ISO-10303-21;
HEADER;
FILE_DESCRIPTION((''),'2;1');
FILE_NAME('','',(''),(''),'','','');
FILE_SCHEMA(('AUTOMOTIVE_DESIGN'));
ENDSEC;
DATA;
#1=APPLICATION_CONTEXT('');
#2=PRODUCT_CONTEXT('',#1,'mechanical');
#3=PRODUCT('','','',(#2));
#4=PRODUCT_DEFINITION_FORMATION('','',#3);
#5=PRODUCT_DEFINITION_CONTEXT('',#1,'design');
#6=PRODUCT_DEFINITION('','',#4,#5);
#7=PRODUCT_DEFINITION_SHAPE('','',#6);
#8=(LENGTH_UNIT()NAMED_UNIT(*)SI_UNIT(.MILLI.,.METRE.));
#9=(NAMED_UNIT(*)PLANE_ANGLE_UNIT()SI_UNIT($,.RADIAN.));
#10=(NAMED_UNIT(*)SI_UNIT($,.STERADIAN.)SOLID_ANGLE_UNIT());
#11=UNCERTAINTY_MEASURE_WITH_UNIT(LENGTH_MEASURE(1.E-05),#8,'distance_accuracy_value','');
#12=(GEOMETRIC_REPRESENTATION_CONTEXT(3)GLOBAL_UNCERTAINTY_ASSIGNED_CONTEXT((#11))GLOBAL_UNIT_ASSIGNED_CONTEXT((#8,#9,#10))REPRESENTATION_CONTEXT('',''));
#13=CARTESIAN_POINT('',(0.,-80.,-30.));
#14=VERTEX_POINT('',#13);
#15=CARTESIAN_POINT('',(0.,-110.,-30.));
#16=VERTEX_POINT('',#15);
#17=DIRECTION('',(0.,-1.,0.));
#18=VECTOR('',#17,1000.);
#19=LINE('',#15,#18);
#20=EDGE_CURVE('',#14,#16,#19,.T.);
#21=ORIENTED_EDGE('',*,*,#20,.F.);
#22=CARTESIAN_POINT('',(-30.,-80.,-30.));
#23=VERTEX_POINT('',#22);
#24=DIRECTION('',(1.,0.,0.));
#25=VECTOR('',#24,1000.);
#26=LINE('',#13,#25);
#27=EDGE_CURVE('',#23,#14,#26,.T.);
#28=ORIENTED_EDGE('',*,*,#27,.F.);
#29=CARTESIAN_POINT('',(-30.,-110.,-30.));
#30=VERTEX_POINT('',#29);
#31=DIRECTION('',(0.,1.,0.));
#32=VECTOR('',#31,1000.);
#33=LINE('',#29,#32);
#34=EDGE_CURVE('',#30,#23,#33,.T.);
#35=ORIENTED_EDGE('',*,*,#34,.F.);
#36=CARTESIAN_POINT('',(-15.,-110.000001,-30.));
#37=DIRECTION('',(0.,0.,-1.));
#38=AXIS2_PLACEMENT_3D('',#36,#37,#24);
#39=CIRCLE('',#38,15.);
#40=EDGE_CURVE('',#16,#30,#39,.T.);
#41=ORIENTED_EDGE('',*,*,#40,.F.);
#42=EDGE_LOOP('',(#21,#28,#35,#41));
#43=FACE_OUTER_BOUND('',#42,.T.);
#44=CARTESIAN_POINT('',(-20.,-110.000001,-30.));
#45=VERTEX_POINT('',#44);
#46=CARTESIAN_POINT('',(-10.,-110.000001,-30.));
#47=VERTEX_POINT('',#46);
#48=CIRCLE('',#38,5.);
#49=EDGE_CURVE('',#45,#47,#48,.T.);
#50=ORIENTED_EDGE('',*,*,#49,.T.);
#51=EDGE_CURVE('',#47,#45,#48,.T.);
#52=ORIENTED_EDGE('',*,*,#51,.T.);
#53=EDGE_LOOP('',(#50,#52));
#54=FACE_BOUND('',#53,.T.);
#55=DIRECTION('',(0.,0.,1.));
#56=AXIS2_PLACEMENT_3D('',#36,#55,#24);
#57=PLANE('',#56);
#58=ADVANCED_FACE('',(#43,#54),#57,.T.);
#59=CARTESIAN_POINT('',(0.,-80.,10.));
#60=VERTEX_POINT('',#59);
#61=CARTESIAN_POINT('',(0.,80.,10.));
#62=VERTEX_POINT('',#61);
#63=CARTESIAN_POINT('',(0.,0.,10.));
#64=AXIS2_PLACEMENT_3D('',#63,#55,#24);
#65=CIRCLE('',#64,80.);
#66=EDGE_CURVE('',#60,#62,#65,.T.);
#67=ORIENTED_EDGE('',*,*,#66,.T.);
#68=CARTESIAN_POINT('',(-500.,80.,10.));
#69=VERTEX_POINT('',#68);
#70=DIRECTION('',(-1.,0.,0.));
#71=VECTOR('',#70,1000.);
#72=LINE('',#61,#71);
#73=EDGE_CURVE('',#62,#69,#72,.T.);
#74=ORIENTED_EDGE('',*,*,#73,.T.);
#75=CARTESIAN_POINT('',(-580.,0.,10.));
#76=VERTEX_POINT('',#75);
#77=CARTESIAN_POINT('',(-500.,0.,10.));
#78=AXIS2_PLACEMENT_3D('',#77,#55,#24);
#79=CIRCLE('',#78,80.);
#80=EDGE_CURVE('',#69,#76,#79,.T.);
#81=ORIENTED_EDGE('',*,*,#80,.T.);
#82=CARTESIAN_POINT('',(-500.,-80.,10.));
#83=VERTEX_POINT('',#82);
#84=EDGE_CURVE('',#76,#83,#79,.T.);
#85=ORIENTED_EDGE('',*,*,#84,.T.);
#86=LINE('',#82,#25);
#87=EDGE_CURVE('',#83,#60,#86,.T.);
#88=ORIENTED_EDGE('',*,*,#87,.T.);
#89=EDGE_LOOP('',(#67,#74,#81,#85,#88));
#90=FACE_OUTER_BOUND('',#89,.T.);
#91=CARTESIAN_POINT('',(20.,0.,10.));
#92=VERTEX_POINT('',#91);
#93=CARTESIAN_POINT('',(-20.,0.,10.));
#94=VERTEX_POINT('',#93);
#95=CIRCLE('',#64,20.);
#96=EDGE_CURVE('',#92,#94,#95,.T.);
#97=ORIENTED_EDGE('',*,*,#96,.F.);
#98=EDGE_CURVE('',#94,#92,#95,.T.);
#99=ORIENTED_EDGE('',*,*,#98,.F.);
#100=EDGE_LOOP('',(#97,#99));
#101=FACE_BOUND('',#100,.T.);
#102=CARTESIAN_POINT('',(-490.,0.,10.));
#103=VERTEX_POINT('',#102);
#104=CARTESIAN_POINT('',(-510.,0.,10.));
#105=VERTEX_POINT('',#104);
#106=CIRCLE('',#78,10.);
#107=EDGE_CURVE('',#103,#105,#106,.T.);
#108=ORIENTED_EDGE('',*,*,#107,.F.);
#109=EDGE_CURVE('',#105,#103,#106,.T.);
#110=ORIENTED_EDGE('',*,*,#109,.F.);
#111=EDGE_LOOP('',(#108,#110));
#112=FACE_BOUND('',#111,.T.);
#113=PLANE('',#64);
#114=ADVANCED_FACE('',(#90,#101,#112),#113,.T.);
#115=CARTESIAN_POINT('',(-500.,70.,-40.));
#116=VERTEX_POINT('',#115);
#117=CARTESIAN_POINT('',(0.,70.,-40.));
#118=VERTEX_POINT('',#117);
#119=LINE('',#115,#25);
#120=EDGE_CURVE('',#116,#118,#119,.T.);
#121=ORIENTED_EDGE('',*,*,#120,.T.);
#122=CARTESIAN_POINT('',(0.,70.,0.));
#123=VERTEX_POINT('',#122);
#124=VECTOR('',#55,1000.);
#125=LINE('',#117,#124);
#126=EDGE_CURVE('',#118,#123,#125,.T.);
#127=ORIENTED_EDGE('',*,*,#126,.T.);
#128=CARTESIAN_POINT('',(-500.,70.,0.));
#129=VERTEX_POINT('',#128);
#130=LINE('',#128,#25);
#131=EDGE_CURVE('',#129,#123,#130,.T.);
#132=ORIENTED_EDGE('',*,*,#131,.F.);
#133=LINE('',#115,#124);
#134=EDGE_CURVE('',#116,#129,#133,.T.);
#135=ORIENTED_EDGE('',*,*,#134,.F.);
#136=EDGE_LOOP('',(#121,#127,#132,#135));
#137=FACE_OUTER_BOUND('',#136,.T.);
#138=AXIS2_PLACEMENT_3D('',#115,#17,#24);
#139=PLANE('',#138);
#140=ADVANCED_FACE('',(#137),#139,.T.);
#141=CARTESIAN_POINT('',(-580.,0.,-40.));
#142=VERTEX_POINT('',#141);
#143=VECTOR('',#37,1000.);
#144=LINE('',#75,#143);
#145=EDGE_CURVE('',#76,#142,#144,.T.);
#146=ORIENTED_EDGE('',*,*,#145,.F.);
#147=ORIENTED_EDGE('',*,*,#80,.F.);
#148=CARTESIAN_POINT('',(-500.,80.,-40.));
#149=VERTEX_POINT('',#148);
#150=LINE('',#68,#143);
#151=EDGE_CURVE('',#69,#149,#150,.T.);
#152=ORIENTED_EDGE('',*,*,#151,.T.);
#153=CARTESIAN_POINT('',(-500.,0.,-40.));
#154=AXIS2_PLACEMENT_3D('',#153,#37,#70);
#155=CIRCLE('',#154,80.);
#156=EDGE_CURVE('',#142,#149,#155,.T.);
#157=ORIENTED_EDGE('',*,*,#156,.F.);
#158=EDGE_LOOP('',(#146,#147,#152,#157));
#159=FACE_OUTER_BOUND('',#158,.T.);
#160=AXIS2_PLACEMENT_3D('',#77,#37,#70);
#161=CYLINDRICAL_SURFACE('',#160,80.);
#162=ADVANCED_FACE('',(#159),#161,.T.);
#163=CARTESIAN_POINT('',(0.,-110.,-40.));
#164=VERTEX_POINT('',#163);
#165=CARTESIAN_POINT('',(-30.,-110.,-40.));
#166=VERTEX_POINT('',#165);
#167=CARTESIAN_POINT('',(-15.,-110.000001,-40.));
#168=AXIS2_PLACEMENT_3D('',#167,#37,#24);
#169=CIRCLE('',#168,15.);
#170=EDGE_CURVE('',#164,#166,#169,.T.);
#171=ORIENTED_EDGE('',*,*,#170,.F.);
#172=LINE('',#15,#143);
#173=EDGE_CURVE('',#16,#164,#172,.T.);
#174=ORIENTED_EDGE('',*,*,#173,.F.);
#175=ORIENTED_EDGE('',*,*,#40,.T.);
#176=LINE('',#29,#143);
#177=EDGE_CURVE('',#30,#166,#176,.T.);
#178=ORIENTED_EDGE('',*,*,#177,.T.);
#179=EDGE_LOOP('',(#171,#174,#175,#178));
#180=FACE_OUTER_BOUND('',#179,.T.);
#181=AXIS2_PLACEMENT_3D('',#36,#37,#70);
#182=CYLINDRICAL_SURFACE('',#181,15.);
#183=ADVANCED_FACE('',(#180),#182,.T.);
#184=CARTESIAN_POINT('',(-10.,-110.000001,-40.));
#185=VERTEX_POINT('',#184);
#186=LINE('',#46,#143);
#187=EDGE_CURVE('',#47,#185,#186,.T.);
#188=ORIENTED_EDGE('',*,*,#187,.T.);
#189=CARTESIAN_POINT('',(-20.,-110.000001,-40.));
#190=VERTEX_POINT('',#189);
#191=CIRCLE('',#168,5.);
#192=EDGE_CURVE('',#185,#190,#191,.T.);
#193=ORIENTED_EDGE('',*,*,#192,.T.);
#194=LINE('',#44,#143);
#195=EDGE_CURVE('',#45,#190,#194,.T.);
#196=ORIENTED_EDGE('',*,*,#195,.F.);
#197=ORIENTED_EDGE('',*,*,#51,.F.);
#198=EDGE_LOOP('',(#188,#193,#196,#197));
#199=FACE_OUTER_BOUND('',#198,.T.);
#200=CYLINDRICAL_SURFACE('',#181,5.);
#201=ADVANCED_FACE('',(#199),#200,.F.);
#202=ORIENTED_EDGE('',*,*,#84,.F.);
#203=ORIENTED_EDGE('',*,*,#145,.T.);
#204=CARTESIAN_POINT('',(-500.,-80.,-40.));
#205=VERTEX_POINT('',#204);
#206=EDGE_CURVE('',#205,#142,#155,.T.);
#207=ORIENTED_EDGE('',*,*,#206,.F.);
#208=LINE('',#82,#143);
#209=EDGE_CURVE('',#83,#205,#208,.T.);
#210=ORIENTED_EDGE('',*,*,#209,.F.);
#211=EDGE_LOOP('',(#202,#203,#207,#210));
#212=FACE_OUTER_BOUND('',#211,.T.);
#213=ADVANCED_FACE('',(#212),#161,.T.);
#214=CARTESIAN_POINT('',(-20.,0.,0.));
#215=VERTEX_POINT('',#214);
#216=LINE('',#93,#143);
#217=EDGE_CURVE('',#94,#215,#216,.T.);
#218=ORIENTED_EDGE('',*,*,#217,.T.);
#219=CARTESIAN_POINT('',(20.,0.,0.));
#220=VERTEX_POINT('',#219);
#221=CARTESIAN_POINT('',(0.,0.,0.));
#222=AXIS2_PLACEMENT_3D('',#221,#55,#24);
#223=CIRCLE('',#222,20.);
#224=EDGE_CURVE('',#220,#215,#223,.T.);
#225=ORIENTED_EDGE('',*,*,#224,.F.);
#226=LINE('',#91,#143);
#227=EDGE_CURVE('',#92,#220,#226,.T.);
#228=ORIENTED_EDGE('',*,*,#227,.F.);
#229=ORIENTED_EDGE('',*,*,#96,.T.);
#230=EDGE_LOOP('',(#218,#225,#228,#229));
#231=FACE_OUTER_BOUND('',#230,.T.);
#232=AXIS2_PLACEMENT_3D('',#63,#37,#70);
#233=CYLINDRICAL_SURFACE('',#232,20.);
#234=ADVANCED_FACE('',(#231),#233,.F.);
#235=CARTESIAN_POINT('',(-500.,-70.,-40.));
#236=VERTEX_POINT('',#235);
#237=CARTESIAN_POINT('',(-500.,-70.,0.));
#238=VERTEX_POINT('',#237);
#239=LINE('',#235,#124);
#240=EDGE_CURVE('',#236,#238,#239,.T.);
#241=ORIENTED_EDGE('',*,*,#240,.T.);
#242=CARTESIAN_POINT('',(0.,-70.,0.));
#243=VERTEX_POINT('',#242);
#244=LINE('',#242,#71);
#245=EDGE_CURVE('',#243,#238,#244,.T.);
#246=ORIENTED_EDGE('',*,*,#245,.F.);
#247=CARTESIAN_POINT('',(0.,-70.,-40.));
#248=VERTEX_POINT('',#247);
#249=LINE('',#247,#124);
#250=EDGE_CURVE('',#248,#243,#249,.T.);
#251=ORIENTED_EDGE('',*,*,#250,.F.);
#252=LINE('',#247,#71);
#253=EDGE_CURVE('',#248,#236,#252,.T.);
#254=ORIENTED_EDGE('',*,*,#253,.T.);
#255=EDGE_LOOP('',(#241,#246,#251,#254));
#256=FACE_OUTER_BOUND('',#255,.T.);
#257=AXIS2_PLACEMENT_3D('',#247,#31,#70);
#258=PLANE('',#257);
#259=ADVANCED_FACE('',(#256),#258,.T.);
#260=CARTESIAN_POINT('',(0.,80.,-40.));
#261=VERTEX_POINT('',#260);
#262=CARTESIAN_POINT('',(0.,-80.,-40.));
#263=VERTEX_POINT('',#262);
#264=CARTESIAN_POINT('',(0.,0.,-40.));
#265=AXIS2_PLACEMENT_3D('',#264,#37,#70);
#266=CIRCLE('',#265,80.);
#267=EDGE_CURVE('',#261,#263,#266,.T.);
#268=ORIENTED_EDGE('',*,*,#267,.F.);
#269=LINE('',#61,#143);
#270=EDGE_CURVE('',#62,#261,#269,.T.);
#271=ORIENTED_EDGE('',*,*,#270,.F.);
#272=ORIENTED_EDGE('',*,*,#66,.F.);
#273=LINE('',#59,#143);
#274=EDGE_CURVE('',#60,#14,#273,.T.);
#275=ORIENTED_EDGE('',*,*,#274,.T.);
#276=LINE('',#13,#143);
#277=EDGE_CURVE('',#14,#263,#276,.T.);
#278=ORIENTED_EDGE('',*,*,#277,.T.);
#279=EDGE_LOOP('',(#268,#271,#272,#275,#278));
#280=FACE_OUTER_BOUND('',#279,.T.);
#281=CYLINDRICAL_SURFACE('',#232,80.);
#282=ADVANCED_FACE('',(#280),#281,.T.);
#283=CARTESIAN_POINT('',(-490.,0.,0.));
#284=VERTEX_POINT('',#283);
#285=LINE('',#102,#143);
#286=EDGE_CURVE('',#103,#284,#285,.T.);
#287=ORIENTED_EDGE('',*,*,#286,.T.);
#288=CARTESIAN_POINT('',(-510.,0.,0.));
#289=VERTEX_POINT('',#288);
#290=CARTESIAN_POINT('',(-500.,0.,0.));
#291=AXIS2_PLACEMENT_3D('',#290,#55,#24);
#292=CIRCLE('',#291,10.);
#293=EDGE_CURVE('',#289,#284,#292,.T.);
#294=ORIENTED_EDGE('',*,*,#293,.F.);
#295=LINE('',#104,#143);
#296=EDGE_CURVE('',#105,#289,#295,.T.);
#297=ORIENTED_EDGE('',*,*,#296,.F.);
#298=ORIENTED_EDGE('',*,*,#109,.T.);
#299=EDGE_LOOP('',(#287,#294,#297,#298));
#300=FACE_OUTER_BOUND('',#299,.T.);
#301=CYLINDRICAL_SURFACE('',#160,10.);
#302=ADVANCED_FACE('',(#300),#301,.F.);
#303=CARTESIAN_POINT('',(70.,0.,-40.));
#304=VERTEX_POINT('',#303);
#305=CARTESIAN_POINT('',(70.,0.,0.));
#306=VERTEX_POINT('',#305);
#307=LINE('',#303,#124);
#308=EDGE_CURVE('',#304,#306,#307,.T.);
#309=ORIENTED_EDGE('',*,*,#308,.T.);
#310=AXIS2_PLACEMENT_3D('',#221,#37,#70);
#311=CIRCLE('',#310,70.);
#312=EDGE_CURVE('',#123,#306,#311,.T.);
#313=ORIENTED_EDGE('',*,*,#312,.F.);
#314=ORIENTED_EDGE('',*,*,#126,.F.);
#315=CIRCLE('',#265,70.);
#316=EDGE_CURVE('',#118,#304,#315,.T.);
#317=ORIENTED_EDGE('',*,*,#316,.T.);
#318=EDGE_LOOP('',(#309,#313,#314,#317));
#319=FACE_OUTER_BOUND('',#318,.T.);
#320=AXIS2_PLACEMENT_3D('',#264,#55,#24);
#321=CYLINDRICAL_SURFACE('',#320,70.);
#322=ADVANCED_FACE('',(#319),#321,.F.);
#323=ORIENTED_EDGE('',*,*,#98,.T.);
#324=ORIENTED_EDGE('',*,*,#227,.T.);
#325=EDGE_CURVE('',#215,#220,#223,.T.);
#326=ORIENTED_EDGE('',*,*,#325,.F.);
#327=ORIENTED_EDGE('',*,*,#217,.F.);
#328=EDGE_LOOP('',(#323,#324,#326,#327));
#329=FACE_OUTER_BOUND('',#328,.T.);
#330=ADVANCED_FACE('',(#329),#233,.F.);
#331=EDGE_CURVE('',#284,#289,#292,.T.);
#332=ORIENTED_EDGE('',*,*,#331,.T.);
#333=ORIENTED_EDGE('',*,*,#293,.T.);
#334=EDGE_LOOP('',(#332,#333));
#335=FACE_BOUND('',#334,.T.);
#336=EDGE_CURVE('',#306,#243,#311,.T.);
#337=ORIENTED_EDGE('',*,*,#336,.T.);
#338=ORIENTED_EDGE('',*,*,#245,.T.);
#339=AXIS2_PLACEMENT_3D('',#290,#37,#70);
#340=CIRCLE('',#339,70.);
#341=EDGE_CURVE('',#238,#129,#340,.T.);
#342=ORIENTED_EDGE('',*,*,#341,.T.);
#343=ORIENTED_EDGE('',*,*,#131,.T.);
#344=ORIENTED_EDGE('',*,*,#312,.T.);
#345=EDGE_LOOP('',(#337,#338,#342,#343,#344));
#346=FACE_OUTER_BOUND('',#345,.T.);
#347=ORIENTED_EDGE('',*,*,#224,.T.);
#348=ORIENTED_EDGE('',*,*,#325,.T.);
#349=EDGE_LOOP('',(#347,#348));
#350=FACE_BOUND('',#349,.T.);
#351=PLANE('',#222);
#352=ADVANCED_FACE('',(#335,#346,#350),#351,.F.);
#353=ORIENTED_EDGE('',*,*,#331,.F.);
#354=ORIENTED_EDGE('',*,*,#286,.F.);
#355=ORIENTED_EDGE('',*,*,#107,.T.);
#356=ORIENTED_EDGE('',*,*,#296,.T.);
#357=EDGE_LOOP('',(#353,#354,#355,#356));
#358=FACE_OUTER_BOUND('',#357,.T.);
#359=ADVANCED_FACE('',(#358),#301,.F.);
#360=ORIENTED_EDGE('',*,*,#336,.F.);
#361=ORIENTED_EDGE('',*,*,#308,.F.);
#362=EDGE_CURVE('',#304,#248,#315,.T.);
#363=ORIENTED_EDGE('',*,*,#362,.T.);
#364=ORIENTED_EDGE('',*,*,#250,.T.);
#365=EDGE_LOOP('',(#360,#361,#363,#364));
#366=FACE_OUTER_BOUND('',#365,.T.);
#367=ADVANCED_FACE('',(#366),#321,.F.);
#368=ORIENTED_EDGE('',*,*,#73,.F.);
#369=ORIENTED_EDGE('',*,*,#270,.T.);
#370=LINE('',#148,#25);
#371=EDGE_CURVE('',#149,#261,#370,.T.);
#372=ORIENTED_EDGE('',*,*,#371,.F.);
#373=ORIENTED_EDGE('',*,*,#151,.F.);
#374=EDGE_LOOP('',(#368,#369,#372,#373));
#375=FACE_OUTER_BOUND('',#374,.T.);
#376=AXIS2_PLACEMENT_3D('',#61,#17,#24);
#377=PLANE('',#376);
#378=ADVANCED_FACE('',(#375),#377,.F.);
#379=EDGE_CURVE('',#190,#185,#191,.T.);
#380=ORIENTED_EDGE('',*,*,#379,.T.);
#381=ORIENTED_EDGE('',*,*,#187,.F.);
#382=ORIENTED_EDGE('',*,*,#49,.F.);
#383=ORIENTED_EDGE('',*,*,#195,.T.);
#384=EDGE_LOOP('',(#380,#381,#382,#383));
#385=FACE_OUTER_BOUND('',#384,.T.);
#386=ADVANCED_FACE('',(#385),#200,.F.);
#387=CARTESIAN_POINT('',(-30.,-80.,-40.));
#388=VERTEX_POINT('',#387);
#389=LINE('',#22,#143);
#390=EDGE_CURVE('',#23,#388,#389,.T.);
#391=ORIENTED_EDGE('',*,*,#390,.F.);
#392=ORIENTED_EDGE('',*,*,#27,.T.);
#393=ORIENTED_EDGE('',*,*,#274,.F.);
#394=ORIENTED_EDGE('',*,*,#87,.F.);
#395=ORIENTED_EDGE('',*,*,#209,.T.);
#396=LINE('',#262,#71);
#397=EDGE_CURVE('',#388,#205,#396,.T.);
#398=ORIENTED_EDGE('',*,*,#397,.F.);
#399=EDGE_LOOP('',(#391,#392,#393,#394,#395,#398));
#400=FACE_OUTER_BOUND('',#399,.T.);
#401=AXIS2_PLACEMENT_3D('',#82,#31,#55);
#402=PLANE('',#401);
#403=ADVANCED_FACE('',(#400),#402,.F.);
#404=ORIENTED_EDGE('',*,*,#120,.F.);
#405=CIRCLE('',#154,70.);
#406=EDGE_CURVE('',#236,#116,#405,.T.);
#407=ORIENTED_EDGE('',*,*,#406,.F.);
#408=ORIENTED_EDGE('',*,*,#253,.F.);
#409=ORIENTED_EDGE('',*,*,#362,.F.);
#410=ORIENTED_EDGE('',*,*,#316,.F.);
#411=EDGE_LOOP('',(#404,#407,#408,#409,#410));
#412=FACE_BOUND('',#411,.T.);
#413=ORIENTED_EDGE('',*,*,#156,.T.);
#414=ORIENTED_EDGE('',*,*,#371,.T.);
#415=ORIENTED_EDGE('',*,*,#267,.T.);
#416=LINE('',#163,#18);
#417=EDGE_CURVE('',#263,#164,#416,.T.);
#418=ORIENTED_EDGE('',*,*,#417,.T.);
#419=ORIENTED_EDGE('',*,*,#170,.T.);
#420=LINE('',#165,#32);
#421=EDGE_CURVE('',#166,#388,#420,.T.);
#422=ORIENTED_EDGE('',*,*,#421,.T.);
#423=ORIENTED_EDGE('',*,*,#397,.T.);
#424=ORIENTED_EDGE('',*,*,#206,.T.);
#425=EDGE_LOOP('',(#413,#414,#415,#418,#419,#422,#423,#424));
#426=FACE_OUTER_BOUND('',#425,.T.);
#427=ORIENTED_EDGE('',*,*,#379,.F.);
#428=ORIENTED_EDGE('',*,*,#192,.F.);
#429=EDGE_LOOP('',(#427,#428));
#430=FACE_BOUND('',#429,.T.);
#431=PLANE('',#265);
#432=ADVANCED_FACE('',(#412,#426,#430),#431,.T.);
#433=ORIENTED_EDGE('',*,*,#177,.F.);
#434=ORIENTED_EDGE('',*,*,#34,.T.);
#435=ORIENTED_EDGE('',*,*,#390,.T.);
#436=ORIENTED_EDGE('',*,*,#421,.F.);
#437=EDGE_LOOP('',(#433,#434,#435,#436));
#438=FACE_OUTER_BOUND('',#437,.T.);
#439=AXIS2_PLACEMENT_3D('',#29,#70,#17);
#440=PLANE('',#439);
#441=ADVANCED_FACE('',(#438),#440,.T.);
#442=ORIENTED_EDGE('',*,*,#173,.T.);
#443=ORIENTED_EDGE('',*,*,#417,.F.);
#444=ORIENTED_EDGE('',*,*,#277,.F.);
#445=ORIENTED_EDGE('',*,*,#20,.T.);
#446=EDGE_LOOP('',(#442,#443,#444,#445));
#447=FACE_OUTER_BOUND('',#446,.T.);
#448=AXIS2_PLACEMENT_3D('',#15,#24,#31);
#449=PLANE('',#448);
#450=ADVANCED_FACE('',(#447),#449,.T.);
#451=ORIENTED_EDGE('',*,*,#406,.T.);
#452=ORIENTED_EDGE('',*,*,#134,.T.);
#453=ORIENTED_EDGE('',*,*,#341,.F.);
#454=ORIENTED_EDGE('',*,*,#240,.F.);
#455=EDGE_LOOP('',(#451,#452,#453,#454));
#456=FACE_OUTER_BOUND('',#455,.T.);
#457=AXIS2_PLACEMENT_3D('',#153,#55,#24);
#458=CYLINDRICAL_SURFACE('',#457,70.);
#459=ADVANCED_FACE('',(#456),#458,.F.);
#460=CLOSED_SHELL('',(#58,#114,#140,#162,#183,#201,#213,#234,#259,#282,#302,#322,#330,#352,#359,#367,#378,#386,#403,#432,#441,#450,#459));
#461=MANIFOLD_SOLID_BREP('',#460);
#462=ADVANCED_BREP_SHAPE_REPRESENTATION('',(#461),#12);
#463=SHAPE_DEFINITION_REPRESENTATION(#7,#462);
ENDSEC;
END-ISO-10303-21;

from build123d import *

# Parameters (mm, degrees)
SKETCH_1_R      = 20
SKETCH_1_R_2    = 10
EXTRUDE_1_DEPTH = 10
EXTRUDE_START   = 40
EXTRUDE_2_DEPTH = 40
SKETCH_4_R      = 5
EXTRUDE_3_DEPTH = 10


with BuildPart() as part:
    # 草图1 → 凸台-拉伸1 (new body)
    with BuildSketch(Plane.XY):
        with BuildLine():
            Line((0, 80), (-500, 80))
            ThreePointArc((-500, 80), (-580, 0), (-500, -80))
            Line((-500, -80), (0, -80))
            ThreePointArc((0, -80), (80, 0), (0, 80))
        make_face()
        Circle(SKETCH_1_R, mode=Mode.SUBTRACT)
        with Locations((-500, 0)):
            Circle(SKETCH_1_R_2, mode=Mode.SUBTRACT)
    extrude(amount=EXTRUDE_1_DEPTH)

    # 草图2 → 凸台-拉伸2 (add)
    with BuildSketch(Plane(origin=(0, 0, 0), x_dir=(-1, 0, 0), z_dir=(0, 0, -1)).offset(EXTRUDE_START)):
        with BuildLine():
            Line((0, -80), (500, -80))
            ThreePointArc((500, -80), (580, 0), (500, 80))
            Line((500, 80), (0, 80))
            ThreePointArc((0, 80), (-80, 0), (0, -80))
        make_face()
        with BuildLine():
            Line((0, -70), (500, -70))
            ThreePointArc((500, -70), (570, 0), (500, 70))
            Line((500, 70), (0, 70))
            ThreePointArc((0, 70), (-70, 0), (0, -70))
        make_face(mode=Mode.SUBTRACT)
    extrude(amount=-EXTRUDE_2_DEPTH)

    # 草图4 → 凸台-拉伸3 (add)
    with BuildSketch(Plane(origin=(0, 0, -40), x_dir=(-1, 0, 0), z_dir=(0, 0, -1))):
        with BuildLine():
            Line((30, -110), (30, -80))
            Line((30, -80), (0, -80))
            Line((0, -80), (0, -110))
            ThreePointArc((0, -110), (15, -125.000001141), (30, -110))
        make_face()
        with Locations(Location((15, -110.000001141, 0), (0, 0, 180))):
            Circle(SKETCH_4_R, mode=Mode.SUBTRACT)
    extrude(amount=-EXTRUDE_3_DEPTH)


solid = part.part
